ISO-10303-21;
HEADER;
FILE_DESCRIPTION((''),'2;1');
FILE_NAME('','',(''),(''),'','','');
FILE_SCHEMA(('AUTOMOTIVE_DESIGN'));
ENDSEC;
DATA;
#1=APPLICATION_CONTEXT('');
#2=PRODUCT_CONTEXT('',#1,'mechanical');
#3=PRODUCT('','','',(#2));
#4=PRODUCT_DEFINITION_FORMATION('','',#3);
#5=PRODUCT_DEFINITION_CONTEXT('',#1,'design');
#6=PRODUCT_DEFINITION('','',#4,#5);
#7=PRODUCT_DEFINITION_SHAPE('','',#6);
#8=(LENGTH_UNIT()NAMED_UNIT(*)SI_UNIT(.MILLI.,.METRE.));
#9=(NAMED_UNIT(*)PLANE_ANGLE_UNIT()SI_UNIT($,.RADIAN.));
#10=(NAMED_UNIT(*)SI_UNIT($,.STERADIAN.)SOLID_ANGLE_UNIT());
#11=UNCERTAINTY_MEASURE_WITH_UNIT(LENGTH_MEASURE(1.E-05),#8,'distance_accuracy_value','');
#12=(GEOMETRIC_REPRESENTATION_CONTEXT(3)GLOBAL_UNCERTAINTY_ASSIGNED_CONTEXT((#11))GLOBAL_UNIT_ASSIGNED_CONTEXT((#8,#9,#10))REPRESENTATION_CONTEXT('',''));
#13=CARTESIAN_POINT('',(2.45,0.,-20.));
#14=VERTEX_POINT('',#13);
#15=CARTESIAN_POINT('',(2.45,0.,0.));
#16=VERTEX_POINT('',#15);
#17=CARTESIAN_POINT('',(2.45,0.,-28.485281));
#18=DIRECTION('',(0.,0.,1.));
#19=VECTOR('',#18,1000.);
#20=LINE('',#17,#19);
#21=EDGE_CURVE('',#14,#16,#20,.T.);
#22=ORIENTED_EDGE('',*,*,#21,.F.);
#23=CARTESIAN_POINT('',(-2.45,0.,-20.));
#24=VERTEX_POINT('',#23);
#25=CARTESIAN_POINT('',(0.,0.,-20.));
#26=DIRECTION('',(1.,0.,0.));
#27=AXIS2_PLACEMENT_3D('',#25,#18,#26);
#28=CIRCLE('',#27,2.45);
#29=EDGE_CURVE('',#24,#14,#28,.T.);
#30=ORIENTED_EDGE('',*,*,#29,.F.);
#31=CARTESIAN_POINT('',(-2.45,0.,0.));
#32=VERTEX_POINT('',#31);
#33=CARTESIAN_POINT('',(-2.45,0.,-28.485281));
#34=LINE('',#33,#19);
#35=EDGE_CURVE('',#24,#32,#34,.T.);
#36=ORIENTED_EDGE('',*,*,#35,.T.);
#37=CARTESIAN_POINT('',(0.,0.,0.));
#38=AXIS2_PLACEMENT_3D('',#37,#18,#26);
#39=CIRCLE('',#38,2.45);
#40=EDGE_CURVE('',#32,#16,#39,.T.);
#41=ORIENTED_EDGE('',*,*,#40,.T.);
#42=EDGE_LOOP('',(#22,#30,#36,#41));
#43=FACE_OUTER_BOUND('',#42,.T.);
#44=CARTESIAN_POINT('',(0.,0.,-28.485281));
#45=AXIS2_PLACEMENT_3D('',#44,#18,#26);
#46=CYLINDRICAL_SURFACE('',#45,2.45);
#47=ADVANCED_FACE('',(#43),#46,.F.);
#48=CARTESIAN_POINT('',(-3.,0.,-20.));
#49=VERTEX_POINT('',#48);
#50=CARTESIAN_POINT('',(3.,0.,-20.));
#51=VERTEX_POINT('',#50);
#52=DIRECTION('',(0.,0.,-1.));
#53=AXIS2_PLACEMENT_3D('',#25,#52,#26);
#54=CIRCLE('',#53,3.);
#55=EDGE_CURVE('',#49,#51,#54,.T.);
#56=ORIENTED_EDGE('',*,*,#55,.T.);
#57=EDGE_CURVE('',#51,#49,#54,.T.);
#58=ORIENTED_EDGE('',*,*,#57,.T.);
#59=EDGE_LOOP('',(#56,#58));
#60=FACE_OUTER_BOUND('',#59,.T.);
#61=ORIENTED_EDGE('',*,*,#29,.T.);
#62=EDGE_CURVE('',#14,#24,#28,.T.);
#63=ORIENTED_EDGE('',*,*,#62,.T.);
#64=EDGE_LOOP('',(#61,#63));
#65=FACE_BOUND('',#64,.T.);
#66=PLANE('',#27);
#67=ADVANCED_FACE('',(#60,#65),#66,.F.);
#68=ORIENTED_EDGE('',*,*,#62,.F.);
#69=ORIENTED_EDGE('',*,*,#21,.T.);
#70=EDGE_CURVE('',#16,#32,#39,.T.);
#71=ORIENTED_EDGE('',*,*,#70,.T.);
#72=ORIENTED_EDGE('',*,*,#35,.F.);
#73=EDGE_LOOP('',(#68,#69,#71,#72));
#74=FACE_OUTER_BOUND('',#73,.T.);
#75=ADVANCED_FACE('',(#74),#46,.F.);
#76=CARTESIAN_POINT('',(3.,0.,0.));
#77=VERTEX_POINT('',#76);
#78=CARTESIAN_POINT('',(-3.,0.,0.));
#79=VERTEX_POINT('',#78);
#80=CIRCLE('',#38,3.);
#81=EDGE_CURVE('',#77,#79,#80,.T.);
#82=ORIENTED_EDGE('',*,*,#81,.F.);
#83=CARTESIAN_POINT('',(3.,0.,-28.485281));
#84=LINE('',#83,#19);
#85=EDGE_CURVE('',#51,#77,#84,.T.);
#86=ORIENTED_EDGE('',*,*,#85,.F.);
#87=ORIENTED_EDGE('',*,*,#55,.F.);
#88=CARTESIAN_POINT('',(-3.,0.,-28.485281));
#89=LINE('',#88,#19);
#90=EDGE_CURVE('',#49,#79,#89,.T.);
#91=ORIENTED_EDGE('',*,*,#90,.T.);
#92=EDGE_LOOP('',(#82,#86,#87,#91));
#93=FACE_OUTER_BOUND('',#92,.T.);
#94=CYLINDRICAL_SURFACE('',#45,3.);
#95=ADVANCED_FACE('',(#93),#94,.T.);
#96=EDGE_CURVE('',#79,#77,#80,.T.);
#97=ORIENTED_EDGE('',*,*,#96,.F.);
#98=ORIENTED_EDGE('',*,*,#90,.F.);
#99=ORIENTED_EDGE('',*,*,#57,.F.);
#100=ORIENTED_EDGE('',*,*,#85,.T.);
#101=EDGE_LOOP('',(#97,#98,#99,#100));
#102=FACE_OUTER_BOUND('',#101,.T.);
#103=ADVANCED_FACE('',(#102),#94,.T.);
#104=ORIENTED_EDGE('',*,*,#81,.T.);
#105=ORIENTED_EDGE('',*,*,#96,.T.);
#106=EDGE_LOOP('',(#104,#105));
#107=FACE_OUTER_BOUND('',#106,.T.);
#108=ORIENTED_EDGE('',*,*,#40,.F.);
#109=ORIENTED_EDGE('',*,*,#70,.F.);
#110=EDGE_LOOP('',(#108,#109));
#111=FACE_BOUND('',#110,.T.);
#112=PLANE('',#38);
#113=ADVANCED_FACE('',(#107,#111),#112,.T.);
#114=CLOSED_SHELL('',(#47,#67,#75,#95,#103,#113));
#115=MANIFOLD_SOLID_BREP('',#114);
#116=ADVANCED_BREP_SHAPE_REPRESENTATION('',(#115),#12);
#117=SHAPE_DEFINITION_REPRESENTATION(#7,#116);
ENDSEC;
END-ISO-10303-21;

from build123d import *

# Parameters (mm, degrees)
SKETCH_1_R      = 3
SKETCH_1_R_2    = 2.45
EXTRUDE_1_DEPTH = 20


with BuildPart() as part:
    # 草图1 → 凸台-拉伸1 (new body)
    with BuildSketch(Plane.XY):
        Circle(SKETCH_1_R)
        Circle(SKETCH_1_R_2, mode=Mode.SUBTRACT)
    extrude(amount=-EXTRUDE_1_DEPTH)


solid = part.part
